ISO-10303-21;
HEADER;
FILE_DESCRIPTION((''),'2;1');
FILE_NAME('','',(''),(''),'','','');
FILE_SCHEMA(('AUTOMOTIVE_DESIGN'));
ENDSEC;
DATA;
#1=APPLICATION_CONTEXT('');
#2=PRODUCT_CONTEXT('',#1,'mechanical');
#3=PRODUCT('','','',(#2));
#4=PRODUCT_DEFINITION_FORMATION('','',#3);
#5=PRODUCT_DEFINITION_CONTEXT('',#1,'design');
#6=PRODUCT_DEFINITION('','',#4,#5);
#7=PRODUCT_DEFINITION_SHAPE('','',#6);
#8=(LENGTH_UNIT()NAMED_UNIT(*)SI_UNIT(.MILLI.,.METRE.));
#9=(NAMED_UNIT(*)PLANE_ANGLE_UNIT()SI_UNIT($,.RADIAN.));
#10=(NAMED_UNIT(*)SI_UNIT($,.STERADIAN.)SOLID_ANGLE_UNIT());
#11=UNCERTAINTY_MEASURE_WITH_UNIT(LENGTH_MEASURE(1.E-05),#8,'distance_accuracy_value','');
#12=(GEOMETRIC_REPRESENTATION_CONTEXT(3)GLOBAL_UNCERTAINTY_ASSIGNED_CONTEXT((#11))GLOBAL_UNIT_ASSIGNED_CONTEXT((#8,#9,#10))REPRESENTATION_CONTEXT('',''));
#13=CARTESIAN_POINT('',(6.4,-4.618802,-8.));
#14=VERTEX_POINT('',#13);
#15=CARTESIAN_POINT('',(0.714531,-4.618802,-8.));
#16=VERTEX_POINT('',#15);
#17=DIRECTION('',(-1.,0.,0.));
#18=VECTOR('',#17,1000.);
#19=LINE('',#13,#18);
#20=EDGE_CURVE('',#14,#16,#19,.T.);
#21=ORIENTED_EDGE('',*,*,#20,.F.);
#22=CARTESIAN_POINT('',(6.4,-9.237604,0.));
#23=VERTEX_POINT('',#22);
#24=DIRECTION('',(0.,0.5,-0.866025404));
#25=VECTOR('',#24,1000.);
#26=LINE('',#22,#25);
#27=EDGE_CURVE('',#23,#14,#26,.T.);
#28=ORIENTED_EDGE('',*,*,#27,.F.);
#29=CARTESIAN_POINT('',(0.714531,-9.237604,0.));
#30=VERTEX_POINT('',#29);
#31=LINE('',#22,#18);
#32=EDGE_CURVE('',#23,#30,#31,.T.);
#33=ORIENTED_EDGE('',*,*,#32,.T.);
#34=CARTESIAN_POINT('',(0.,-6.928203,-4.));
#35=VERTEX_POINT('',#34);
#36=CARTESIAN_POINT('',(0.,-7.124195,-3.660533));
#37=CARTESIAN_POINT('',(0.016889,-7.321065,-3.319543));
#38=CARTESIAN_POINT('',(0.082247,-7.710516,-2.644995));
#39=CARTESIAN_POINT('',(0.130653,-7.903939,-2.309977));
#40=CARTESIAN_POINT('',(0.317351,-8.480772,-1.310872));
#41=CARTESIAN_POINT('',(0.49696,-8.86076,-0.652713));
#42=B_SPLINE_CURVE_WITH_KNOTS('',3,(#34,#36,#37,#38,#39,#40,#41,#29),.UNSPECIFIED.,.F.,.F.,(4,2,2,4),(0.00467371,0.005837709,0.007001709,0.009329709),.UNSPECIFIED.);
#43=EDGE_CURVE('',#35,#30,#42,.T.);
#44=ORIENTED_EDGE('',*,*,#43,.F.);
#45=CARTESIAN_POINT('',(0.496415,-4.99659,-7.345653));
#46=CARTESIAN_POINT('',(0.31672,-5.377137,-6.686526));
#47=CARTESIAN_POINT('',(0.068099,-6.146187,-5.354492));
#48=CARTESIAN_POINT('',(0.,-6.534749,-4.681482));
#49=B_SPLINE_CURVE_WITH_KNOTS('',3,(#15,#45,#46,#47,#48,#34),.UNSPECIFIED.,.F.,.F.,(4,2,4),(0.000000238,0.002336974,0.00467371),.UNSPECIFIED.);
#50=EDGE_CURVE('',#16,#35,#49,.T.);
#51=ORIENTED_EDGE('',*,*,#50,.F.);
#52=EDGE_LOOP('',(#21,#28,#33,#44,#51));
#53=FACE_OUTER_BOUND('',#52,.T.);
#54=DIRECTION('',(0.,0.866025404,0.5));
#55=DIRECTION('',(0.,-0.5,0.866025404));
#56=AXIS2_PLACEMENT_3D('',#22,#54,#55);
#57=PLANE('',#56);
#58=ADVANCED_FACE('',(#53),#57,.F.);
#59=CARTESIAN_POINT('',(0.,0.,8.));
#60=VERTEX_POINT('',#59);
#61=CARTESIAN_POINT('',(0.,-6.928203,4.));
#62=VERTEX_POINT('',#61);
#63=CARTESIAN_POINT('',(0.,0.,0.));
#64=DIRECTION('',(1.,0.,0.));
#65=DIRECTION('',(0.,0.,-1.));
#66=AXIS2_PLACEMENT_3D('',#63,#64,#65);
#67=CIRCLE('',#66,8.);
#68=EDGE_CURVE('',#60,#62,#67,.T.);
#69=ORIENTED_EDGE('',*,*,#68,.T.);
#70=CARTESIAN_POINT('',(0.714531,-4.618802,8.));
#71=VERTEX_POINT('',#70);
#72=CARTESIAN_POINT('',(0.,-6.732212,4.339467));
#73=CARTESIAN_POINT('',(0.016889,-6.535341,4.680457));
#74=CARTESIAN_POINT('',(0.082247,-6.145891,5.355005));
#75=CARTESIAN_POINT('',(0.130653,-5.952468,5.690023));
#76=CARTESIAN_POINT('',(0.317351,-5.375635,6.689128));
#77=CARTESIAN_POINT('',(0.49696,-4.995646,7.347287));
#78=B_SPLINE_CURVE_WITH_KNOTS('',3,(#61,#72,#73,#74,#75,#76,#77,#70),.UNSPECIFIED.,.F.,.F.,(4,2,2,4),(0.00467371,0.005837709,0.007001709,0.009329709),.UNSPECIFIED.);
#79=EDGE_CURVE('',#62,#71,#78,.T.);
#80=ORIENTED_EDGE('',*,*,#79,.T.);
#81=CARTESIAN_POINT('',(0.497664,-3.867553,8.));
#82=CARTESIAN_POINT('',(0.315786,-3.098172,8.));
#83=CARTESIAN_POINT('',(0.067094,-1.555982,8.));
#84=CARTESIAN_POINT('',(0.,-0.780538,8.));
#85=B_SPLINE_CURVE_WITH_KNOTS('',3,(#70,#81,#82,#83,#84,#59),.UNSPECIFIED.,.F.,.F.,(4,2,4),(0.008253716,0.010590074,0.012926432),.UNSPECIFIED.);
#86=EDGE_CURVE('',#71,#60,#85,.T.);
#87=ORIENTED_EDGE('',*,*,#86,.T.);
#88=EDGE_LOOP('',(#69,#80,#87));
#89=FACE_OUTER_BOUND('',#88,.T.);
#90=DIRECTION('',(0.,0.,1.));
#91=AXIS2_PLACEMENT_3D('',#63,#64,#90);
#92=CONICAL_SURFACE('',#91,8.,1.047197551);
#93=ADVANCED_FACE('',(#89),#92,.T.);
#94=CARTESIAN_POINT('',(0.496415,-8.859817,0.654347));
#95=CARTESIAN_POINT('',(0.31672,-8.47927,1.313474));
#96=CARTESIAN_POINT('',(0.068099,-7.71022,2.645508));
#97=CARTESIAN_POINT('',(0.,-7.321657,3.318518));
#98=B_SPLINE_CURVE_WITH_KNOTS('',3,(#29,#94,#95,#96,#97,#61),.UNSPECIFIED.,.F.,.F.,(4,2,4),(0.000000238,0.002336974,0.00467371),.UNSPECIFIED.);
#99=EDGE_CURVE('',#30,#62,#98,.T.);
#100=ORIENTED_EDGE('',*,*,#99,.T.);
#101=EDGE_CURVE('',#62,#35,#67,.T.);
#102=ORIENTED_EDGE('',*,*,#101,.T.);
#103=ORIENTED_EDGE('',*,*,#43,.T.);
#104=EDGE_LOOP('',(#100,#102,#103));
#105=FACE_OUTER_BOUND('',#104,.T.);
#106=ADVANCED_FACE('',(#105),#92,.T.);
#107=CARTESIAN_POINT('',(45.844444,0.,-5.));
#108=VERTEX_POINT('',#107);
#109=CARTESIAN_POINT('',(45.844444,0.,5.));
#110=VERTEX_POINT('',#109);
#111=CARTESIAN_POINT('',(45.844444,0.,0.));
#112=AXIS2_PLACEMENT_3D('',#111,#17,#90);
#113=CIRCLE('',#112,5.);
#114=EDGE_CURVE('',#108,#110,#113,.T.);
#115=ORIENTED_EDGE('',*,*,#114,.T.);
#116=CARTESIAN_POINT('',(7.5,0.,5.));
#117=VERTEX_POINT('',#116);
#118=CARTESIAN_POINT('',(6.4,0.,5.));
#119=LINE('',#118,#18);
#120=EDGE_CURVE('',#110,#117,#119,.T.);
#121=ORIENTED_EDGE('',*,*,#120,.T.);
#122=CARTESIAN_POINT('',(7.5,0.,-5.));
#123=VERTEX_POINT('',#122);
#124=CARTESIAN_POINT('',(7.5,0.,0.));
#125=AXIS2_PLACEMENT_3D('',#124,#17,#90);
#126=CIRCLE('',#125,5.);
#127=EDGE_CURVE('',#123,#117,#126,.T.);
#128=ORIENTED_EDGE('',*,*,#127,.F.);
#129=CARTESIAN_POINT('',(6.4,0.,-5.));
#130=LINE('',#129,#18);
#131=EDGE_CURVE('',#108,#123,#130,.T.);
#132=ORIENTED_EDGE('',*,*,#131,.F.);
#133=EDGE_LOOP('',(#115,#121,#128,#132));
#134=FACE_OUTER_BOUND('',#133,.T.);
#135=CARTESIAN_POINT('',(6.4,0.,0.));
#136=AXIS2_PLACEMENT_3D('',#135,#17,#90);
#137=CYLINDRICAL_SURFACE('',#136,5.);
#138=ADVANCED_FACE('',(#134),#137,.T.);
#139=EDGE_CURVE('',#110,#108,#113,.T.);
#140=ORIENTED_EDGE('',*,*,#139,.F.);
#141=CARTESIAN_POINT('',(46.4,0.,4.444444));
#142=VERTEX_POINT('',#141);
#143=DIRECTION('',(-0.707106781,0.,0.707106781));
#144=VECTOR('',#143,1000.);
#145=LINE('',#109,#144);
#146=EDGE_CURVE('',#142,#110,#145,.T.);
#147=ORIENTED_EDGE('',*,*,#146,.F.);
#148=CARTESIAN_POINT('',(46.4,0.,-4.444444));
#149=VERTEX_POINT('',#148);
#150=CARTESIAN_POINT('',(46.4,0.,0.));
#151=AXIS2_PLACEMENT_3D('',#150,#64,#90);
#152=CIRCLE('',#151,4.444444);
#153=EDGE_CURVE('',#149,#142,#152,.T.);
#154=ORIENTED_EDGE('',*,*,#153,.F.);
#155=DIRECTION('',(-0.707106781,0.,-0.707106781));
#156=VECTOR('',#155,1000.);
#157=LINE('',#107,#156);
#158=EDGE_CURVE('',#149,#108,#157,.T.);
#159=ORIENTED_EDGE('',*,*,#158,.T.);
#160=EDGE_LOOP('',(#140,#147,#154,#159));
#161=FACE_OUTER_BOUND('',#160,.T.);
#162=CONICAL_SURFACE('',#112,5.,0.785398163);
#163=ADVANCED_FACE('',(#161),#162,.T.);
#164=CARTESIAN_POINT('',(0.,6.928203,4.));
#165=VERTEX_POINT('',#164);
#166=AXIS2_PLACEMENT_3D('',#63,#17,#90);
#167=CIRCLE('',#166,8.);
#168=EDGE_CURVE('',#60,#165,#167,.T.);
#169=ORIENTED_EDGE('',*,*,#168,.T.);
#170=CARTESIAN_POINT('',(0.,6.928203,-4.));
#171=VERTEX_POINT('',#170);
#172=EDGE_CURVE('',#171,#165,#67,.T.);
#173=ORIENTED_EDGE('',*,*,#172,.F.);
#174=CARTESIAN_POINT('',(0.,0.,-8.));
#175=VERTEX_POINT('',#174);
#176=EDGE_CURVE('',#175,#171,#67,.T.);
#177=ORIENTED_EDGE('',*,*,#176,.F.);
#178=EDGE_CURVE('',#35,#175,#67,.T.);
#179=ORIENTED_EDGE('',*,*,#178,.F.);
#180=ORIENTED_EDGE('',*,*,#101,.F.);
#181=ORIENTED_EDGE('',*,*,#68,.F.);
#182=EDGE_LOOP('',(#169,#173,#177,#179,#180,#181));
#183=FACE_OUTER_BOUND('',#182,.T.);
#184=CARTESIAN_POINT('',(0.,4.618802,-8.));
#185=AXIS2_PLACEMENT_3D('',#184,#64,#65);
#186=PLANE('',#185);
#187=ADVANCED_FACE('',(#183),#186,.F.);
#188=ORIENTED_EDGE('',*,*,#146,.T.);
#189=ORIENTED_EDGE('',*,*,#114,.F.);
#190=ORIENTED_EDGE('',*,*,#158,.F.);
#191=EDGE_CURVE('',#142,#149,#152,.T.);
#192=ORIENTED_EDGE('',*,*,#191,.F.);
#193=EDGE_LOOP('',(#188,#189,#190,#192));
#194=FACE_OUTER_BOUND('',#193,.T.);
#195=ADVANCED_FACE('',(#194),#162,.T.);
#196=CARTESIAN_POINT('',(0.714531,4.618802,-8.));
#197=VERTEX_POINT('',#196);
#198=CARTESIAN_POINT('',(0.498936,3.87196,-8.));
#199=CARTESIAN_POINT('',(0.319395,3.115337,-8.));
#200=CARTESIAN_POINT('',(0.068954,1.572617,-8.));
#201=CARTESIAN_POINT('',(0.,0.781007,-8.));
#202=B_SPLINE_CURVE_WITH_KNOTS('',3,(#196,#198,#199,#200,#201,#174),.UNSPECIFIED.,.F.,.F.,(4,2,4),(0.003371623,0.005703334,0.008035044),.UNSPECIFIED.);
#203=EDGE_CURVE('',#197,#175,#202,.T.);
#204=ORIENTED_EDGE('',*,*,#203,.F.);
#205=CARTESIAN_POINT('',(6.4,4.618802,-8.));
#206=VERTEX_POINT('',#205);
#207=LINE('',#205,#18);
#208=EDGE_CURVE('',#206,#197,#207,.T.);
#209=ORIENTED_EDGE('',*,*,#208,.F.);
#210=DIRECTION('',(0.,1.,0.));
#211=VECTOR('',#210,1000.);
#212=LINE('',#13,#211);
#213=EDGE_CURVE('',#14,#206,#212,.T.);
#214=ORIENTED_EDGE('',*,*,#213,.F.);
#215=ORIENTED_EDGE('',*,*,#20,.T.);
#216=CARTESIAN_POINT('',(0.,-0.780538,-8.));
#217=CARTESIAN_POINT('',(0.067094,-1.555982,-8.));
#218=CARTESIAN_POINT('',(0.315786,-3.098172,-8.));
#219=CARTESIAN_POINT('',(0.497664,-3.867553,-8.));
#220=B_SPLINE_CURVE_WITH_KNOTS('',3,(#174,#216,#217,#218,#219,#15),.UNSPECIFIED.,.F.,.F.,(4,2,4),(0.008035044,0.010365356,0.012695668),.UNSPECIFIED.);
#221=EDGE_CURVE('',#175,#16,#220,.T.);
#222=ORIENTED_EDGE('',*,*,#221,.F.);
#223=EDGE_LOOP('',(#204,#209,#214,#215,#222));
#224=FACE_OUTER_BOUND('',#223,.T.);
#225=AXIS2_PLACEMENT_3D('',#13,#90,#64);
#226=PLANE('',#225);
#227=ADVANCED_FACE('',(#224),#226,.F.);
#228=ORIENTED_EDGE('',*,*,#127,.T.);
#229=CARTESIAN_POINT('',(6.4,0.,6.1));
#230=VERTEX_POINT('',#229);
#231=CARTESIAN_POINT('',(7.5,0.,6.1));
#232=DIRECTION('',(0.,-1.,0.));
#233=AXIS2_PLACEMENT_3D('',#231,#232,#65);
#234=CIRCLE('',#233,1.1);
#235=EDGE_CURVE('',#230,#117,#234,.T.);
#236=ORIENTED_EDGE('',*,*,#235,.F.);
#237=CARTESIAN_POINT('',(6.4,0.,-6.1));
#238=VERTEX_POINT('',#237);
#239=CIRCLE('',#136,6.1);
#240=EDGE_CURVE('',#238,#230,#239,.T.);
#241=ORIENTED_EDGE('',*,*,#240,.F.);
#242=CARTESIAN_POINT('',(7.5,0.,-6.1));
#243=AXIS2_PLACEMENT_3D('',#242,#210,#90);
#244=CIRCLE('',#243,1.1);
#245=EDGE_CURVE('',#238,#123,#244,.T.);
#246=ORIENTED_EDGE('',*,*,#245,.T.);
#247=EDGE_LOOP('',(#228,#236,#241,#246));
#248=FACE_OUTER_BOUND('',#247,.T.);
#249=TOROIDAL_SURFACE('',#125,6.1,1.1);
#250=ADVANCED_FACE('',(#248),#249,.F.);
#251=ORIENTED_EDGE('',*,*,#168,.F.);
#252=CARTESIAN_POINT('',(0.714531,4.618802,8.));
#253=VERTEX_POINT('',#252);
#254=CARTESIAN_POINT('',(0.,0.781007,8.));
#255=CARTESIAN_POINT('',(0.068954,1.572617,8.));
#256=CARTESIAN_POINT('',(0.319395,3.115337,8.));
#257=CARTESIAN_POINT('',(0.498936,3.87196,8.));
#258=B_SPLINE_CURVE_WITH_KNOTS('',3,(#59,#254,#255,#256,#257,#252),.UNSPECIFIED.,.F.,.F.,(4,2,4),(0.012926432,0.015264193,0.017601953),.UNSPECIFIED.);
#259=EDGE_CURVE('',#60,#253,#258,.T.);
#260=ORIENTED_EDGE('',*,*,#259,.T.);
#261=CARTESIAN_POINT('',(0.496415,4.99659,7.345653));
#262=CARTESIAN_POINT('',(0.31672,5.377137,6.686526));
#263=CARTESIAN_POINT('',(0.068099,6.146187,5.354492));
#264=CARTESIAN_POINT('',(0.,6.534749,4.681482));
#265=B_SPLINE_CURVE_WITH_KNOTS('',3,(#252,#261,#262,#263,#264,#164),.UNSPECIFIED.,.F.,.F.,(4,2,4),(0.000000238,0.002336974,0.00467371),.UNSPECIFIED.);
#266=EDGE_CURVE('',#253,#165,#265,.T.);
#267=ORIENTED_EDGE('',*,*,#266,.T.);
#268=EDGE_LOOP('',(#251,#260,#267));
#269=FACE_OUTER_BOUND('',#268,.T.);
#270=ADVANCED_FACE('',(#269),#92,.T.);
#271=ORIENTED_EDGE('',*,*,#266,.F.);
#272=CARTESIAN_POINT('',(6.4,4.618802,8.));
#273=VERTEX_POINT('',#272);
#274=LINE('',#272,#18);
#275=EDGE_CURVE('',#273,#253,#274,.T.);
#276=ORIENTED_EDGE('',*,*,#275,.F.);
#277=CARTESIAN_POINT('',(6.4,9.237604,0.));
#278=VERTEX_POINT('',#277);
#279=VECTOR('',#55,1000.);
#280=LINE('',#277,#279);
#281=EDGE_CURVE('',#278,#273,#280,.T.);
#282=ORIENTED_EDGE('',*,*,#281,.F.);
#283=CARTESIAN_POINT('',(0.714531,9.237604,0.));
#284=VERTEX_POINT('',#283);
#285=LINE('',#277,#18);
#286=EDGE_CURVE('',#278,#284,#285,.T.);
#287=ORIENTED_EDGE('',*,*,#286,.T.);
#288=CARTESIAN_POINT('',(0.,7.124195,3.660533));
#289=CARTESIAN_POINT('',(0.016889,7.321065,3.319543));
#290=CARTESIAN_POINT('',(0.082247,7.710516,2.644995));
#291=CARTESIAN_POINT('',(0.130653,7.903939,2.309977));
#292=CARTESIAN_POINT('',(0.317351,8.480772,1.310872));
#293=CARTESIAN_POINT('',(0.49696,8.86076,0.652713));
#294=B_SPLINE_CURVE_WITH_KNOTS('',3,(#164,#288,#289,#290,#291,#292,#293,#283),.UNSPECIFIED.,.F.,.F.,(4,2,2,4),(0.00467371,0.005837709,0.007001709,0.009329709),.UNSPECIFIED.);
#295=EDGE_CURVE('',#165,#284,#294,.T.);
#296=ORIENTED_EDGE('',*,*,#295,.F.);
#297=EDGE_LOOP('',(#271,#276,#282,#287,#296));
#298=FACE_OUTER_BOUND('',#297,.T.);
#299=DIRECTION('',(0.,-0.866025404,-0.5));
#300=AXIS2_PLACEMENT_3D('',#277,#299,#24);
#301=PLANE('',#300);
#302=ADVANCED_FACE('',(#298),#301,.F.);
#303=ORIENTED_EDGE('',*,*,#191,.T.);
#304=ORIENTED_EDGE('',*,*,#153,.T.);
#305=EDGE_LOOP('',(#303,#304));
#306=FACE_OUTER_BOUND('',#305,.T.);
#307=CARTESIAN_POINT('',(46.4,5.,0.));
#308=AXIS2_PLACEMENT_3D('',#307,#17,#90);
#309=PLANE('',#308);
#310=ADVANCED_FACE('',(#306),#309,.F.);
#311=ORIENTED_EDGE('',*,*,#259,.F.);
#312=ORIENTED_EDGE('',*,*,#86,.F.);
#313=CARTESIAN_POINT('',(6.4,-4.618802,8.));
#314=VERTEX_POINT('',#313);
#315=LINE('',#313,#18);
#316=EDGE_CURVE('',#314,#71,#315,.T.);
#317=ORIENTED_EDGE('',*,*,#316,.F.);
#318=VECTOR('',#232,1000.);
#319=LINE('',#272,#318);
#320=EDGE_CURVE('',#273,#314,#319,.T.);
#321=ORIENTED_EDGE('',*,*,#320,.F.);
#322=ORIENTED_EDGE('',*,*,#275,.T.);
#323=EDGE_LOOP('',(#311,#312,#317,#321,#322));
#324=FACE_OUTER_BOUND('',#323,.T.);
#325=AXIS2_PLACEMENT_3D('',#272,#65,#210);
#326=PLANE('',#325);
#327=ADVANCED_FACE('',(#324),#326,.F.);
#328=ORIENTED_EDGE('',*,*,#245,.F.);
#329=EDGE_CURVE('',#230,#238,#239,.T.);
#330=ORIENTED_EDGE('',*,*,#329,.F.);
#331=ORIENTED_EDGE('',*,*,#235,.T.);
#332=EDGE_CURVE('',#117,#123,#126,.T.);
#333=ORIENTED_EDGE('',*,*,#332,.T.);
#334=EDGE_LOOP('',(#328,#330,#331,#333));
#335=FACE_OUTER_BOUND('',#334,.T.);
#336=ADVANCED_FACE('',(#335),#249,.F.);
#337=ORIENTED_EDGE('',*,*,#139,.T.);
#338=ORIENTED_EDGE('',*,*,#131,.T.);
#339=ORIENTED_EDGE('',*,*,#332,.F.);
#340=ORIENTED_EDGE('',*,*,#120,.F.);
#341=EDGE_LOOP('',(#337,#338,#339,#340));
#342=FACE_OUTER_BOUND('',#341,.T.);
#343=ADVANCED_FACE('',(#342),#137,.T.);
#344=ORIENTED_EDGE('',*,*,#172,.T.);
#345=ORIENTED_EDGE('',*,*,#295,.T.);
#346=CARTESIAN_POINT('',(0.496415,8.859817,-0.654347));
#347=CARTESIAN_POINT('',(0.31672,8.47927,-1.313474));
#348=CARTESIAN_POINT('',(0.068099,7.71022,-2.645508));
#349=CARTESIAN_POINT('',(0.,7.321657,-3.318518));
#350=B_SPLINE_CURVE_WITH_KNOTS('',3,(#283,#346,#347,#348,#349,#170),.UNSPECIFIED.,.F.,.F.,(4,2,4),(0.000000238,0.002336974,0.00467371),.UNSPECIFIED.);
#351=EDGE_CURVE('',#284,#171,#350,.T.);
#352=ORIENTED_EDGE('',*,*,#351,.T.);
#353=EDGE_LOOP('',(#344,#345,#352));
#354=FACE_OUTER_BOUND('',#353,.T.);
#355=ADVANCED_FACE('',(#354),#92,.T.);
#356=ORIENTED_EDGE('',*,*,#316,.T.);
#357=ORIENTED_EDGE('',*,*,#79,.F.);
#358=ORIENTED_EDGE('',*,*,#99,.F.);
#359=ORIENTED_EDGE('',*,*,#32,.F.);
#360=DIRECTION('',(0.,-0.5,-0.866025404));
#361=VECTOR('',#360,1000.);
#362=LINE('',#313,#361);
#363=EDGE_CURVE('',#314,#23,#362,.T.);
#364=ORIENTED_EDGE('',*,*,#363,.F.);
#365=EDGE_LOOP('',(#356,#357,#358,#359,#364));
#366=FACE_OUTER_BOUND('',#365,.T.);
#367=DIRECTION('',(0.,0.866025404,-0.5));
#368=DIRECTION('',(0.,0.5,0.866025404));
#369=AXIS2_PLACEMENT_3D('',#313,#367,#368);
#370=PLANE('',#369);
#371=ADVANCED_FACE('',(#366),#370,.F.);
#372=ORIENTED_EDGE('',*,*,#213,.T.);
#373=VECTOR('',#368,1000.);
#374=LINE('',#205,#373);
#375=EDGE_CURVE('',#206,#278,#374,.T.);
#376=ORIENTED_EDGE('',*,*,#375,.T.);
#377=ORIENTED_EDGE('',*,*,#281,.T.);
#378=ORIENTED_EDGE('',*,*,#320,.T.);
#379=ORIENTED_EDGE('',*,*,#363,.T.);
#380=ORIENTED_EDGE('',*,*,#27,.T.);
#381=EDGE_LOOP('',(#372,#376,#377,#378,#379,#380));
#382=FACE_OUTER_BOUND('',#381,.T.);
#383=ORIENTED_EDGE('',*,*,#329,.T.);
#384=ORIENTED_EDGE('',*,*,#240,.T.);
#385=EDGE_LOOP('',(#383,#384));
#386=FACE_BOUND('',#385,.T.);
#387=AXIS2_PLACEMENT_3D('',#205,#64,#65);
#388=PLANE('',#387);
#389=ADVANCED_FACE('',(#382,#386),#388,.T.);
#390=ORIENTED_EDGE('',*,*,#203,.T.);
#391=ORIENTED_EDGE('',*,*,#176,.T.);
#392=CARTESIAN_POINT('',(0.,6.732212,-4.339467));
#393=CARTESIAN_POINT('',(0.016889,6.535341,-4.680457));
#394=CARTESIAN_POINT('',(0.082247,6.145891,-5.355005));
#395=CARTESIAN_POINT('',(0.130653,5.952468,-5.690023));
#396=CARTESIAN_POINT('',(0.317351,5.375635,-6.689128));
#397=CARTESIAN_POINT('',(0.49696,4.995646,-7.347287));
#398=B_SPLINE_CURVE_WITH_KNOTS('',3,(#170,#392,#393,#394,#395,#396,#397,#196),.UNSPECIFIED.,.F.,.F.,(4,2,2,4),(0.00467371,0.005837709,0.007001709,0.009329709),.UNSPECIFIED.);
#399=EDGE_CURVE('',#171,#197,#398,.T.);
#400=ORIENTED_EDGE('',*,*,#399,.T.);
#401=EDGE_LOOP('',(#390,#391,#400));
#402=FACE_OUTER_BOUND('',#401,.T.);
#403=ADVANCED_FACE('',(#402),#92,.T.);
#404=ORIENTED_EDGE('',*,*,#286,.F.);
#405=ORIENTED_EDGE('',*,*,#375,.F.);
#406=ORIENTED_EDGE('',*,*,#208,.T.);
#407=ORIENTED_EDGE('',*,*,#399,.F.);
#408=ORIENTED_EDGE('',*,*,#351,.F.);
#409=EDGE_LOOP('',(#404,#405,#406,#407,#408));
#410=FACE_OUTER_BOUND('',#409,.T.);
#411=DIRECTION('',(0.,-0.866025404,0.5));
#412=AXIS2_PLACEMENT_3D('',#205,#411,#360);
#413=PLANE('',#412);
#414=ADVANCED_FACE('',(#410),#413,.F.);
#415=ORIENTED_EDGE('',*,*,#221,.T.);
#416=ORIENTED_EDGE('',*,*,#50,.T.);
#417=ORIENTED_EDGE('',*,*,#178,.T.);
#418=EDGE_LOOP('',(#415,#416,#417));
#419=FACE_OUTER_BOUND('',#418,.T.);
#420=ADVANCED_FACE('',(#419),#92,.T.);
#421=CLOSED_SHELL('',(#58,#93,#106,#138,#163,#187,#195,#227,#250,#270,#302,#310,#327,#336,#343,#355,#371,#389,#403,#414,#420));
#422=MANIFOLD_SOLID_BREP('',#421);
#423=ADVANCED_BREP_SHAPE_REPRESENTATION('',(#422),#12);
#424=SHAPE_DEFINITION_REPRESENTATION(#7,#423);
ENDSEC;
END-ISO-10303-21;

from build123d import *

# Parameters (mm, degrees)
BOSS_EXTRUDE1_DEPTH = 6.4
SKETCH4_R           = 17.59
SKETCH4_R_2         = 8
CUT_EXTRUDE1_DEPTH  = 0.8
CUT_EXTRUDE1_DRAFT  = -60
CHAMFER2_SIZE       = 0.555555556


with BuildPart() as part:
    # Sketch3 → Boss-Extrude1 (new body)
    with BuildSketch(Plane(origin=(0, 0, 0), x_dir=(0, 0, -1), z_dir=(1, 0, 0))):
        Polygon((8, 4.618802154), (0, 9.237604307), (-8, 4.618802154), (-8, -4.618802154), (0, -9.237604307), (8, -4.618802154), align=None)
    extrude(amount=BOSS_EXTRUDE1_DEPTH)


with BuildPart() as cut_extrude1_tool:
    # Sketch4 → Cut-Extrude1 (with draft: the straight prism first)
    with BuildSketch(Plane.ZY):
        Circle(SKETCH4_R)
        Circle(SKETCH4_R_2, mode=Mode.SUBTRACT)
    extrude(amount=-CUT_EXTRUDE1_DEPTH)
    # Cut-Extrude1: the draft: its side faces are tilted about the plane it starts from
    cut_extrude1_sides = [cut_extrude1_tool.faces().sort_by_distance(p)[0] for p in [
        (0.4, 0, -17.59),
        (0.4, 0, -8),
    ]]
    draft(cut_extrude1_sides, Plane.ZY, CUT_EXTRUDE1_DRAFT)


with BuildPart() as part_1:
    add(part.part)

    # Cut-Extrude1: cut by cut_extrude1_tool
    add(cut_extrude1_tool.part, mode=Mode.SUBTRACT)

    # Sketch5 → Revolve1 (revolve)
    with BuildSketch(Plane.XY, mode=Mode.PRIVATE) as revolve1_sk:
        with BuildLine():
            Line((7.5, 5), (46.4, 5))
            Line((46.4, 5), (46.4, 0))
            Line((46.4, 0), (6.4, 0))
            Line((6.4, 0), (6.4, 6.1))
            ThreePointArc((6.4, 6.1), (6.722182541, 5.322182541), (7.5, 5))
        make_face()
    revolve(revolve1_sk.sketch.rotate(Axis((6.4, 0, 0), (1, 0, 0)), 90), axis=Axis((6.4, 0, 0), (1, 0, 0)))

    # Chamfer2
    chamfer2_edges = [part_1.edges().sort_by_distance(p)[0] for p in [
        (46.4, 0, -5),
    ]]
    chamfer(chamfer2_edges, length=CHAMFER2_SIZE)


solid = part_1.part
